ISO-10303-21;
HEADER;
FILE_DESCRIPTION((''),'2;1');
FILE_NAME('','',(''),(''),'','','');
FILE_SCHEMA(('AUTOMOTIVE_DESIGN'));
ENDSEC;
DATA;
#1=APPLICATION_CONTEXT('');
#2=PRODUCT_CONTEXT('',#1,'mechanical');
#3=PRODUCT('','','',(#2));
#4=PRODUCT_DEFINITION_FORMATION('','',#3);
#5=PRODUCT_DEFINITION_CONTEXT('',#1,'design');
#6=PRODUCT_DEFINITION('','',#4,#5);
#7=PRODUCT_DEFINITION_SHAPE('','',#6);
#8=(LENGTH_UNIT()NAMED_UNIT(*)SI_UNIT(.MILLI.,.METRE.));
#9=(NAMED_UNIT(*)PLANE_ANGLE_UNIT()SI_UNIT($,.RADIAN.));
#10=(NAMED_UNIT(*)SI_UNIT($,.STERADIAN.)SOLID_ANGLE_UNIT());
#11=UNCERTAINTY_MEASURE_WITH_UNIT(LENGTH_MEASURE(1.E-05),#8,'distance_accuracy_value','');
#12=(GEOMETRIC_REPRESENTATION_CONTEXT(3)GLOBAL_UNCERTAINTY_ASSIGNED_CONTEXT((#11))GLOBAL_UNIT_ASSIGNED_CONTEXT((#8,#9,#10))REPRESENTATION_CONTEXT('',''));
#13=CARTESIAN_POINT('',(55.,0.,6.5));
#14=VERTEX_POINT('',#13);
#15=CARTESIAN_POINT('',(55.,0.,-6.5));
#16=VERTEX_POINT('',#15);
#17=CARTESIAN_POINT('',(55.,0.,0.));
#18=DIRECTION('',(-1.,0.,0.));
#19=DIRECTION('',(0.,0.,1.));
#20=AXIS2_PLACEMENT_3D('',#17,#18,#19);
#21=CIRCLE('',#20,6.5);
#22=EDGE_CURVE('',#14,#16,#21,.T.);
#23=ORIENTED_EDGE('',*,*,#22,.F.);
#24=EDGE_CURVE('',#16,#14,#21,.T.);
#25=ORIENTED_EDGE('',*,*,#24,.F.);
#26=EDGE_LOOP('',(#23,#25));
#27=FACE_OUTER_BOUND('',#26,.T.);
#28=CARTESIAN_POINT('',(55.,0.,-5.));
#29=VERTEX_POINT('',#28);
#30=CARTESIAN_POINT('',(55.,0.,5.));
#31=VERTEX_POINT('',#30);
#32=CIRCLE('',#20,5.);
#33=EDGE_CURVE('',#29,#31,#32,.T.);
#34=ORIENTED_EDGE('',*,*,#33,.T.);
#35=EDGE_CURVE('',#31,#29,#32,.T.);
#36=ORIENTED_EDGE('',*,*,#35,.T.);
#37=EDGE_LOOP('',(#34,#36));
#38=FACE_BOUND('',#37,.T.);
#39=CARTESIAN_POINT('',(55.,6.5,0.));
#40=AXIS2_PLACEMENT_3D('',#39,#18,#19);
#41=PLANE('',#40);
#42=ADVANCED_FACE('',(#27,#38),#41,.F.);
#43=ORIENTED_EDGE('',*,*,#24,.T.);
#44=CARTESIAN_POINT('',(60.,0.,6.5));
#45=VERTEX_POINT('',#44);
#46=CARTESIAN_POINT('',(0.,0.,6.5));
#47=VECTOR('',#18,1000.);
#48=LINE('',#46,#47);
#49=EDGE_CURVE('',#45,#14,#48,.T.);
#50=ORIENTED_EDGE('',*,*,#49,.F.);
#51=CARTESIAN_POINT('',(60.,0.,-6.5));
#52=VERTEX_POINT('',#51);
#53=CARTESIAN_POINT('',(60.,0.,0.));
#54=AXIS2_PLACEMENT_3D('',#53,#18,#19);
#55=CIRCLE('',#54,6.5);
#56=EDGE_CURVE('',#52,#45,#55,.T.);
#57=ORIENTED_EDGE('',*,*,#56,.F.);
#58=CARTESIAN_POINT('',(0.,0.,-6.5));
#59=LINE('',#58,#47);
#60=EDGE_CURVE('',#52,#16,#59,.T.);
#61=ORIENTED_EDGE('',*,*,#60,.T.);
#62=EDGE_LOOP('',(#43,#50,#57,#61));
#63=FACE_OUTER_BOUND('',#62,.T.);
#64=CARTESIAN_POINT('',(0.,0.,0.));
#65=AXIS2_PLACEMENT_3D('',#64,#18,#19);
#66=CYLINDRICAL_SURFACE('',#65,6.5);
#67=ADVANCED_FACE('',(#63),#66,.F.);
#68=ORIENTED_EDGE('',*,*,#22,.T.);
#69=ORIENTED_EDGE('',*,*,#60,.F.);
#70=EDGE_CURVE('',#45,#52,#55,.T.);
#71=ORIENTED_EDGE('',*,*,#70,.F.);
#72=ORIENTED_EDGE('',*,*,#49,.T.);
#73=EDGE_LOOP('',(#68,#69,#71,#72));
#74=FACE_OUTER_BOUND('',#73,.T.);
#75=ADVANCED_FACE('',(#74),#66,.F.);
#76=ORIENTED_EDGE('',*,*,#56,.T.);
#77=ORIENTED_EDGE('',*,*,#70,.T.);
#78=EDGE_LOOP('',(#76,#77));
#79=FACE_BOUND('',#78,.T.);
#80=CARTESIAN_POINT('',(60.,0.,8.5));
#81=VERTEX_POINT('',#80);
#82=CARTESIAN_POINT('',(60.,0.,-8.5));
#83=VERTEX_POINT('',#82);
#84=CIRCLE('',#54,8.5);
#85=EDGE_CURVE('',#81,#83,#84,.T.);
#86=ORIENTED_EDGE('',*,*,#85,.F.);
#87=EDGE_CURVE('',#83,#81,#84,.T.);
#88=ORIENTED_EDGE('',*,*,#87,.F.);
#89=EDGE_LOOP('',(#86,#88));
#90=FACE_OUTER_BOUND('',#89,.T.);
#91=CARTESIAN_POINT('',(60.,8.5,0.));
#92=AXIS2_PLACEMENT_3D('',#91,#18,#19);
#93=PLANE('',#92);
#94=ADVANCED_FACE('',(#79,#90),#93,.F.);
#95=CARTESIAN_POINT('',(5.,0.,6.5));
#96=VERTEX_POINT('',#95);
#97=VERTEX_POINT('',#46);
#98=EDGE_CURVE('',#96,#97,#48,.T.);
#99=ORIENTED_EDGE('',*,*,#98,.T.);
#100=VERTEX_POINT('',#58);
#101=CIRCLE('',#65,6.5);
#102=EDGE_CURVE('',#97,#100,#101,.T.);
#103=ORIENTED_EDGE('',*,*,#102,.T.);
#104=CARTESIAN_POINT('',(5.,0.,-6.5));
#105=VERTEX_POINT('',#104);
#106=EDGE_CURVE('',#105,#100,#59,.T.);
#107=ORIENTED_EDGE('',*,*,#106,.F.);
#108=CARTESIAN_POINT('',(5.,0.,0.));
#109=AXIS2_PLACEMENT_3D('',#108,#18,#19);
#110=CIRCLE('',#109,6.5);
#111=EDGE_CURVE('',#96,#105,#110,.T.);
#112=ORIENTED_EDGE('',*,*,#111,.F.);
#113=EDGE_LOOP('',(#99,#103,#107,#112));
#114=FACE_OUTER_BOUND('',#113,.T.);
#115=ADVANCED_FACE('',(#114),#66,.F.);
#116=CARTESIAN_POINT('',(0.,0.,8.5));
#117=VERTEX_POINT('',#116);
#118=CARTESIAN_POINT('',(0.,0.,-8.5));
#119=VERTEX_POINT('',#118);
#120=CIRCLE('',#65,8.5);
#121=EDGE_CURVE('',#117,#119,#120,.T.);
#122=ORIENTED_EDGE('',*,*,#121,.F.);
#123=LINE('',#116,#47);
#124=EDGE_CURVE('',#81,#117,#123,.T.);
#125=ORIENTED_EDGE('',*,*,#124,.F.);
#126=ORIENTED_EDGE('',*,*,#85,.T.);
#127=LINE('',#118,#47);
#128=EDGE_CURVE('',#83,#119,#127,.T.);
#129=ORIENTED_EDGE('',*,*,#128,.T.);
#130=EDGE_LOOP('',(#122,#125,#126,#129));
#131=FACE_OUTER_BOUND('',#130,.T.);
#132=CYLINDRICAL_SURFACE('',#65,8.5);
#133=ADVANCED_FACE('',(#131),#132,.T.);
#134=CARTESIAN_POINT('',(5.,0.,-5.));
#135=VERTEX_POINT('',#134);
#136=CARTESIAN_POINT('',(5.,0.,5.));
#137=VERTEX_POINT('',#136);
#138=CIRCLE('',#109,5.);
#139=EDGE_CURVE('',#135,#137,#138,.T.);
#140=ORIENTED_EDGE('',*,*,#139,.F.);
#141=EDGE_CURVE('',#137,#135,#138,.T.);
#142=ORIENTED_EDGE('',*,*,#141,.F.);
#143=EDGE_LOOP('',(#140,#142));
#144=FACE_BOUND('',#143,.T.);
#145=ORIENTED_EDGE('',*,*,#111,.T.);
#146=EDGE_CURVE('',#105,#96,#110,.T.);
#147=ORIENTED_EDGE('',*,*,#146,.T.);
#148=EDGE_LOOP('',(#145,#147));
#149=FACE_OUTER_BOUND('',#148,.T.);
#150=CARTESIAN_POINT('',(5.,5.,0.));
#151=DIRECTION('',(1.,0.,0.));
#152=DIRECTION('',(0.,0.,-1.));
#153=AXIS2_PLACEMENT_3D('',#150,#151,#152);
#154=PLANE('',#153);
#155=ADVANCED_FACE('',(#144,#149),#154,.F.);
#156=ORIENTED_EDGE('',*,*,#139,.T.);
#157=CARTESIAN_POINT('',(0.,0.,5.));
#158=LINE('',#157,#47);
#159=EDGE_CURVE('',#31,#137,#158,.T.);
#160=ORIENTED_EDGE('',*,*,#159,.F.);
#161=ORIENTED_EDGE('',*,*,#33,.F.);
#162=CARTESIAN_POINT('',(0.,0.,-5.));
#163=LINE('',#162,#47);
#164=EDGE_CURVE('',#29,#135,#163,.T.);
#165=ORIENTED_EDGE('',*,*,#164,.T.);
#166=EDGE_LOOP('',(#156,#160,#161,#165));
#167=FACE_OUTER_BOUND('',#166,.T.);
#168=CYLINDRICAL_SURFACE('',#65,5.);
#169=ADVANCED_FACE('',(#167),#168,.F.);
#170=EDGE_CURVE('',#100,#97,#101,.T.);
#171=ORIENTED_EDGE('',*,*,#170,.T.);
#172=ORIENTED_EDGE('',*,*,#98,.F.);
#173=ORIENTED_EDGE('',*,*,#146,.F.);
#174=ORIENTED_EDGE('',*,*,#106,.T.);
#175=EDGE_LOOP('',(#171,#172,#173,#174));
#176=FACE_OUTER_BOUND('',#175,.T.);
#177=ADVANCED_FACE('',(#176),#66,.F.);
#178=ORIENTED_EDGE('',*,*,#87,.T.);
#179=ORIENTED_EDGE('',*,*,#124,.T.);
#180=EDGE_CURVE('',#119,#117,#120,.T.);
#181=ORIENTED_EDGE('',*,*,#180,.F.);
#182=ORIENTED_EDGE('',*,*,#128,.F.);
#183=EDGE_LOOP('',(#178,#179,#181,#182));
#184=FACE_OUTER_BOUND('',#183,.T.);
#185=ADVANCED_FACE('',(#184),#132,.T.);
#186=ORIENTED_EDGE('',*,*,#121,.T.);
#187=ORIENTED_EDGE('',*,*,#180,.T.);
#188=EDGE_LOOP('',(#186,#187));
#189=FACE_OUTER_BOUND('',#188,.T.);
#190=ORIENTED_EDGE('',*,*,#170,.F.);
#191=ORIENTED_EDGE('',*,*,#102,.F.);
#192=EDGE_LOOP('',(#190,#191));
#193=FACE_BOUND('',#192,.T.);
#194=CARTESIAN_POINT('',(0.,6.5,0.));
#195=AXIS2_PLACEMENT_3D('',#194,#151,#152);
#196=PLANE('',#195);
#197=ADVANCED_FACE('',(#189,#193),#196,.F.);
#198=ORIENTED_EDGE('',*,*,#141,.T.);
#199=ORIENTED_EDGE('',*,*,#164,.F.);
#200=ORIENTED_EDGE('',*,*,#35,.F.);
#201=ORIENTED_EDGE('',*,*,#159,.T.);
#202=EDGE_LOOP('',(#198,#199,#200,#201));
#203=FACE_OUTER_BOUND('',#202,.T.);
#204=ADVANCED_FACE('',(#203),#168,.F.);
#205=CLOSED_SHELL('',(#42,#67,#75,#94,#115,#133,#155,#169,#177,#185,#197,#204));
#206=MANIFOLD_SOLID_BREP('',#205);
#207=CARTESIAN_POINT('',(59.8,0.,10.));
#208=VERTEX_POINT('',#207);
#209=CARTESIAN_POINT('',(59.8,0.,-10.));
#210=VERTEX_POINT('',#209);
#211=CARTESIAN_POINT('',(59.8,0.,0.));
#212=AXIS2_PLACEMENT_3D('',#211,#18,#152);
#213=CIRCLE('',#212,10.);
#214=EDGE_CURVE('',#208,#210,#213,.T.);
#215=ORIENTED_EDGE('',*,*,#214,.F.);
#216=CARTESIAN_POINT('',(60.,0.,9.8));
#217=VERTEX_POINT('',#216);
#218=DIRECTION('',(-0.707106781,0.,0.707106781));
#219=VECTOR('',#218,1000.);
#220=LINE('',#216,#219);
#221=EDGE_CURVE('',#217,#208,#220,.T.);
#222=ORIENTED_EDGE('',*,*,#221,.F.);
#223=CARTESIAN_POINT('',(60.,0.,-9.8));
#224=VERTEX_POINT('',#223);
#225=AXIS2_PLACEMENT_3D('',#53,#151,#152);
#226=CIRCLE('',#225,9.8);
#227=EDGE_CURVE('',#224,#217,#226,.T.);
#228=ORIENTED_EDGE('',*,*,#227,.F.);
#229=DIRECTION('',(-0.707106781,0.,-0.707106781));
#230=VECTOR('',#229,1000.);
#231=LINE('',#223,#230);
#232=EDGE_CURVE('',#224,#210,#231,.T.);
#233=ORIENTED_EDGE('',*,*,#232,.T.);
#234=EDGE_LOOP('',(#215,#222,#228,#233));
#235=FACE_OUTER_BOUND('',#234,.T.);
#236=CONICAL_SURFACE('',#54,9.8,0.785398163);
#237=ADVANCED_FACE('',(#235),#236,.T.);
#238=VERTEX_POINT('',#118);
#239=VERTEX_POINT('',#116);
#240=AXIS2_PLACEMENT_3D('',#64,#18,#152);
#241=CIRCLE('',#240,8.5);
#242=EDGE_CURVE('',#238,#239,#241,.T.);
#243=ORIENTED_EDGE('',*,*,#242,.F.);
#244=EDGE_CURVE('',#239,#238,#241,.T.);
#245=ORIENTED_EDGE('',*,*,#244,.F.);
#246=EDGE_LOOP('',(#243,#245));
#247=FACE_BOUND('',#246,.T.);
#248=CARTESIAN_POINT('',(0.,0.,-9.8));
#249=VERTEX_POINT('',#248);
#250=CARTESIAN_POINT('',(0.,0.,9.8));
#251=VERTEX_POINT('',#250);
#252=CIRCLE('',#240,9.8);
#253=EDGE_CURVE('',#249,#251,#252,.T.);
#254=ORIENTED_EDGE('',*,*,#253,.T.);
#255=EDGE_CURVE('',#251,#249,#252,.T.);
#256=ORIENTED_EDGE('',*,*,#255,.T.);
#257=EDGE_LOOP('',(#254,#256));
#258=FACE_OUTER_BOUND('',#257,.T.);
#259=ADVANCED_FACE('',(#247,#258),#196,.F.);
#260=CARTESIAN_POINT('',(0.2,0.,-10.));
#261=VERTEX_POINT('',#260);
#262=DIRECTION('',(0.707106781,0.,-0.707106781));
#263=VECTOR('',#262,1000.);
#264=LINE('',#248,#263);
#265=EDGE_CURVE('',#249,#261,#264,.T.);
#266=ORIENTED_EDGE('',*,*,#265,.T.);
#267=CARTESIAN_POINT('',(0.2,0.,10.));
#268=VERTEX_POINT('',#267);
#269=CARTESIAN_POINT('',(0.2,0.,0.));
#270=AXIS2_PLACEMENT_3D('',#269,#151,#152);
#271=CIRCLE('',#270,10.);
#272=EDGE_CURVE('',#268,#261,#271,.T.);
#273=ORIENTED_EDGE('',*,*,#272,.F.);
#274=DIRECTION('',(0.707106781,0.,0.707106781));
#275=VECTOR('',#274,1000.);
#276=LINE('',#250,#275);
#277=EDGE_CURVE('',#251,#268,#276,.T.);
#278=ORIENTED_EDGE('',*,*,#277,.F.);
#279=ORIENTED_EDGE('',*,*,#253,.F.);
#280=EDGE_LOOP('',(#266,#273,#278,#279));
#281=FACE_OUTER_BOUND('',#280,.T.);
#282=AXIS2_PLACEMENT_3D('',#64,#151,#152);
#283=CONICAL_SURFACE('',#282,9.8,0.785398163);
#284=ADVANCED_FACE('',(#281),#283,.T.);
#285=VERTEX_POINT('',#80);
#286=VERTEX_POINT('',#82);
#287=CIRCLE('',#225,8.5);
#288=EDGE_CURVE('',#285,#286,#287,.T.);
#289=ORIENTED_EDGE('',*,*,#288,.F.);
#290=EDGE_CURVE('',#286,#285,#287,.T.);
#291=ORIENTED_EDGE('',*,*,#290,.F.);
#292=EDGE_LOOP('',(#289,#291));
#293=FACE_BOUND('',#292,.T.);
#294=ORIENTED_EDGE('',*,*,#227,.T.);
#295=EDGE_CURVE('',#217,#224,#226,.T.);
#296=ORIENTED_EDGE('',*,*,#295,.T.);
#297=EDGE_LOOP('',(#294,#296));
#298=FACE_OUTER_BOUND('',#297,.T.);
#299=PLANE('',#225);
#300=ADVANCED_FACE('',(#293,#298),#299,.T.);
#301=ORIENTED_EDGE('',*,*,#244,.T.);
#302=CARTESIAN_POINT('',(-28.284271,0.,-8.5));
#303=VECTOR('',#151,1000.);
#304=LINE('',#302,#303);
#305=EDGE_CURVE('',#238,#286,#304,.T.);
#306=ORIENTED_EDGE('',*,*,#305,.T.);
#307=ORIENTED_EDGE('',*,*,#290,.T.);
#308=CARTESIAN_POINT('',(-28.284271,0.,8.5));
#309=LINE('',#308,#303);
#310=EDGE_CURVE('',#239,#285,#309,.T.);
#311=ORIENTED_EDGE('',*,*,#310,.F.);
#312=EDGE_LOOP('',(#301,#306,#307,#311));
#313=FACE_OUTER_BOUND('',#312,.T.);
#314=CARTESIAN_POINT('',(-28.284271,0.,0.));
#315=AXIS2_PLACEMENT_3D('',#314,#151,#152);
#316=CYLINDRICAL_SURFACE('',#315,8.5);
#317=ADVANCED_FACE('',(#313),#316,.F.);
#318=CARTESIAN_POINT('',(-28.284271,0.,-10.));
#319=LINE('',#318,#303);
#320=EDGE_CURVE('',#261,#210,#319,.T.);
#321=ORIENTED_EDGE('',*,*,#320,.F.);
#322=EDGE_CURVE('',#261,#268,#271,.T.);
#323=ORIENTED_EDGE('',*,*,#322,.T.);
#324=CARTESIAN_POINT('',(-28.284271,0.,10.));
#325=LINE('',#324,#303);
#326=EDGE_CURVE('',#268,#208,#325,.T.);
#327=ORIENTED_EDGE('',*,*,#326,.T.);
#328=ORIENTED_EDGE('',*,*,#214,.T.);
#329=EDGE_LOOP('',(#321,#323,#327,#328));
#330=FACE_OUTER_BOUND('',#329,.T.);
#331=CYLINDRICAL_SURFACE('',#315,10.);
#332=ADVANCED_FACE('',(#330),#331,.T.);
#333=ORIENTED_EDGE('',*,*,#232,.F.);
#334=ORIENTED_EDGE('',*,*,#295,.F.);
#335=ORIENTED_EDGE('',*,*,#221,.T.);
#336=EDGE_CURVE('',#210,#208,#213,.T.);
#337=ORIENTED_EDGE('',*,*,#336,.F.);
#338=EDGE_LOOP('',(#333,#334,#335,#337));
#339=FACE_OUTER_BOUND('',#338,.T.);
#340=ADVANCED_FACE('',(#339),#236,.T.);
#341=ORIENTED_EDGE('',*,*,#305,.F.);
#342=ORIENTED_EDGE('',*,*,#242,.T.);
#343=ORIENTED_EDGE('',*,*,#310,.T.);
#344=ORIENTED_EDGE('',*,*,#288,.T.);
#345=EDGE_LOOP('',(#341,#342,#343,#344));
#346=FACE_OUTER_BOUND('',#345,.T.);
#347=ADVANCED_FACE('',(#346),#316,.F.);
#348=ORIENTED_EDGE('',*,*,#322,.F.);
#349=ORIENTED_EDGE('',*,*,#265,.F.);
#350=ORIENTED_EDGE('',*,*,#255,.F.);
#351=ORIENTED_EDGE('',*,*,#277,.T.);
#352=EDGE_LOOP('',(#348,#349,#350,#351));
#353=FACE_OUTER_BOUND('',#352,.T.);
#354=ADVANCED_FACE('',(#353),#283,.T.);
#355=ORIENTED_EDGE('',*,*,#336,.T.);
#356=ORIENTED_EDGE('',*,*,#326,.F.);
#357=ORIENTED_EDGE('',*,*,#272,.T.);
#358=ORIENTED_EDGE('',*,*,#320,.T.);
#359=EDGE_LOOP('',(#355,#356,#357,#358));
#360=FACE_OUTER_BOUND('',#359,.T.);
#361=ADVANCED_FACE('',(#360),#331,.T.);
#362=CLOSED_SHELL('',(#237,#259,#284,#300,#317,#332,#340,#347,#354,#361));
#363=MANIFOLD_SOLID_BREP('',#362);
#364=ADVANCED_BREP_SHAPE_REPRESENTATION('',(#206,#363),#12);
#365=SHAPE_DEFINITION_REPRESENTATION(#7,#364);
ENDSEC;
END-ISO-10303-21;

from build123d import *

# Parameters (mm, degrees)
SKETCH2_R           = 10
SKETCH2_R_2         = 8.5
BOSS_EXTRUDE1_DEPTH = 60
CHAMFER1_SIZE       = 0.2


with BuildPart() as part:
    # Sketch1 → Revolve1 (revolve)
    with BuildSketch(Plane.XY, mode=Mode.PRIVATE) as revolve1_sk:
        Polygon((0, 8.5), (60, 8.5), (60, 6.5), (55, 6.5), (55, 5), (5, 5), (5, 6.5), (0, 6.5), align=None)
    revolve(revolve1_sk.sketch.rotate(Axis((0, 0, 0), (1, 0, 0)), 90), axis=Axis((0, 0, 0), (1, 0, 0)))


with BuildPart() as body_2:
    # Sketch2 → Boss-Extrude1 (new body)
    with BuildSketch(Plane(origin=(60, 0, 0), x_dir=(0, 0, -1), z_dir=(1, 0, 0))):
        Circle(SKETCH2_R)
        Circle(SKETCH2_R_2, mode=Mode.SUBTRACT)
    extrude(amount=-BOSS_EXTRUDE1_DEPTH)

    # Chamfer1
    chamfer1_edges = [body_2.edges().sort_by_distance(p)[0] for p in [
        (60, 0, 10),
        (0, 0, 10),
    ]]
    chamfer(chamfer1_edges, length=CHAMFER1_SIZE)


solid = Compound([part.part, body_2.part])
